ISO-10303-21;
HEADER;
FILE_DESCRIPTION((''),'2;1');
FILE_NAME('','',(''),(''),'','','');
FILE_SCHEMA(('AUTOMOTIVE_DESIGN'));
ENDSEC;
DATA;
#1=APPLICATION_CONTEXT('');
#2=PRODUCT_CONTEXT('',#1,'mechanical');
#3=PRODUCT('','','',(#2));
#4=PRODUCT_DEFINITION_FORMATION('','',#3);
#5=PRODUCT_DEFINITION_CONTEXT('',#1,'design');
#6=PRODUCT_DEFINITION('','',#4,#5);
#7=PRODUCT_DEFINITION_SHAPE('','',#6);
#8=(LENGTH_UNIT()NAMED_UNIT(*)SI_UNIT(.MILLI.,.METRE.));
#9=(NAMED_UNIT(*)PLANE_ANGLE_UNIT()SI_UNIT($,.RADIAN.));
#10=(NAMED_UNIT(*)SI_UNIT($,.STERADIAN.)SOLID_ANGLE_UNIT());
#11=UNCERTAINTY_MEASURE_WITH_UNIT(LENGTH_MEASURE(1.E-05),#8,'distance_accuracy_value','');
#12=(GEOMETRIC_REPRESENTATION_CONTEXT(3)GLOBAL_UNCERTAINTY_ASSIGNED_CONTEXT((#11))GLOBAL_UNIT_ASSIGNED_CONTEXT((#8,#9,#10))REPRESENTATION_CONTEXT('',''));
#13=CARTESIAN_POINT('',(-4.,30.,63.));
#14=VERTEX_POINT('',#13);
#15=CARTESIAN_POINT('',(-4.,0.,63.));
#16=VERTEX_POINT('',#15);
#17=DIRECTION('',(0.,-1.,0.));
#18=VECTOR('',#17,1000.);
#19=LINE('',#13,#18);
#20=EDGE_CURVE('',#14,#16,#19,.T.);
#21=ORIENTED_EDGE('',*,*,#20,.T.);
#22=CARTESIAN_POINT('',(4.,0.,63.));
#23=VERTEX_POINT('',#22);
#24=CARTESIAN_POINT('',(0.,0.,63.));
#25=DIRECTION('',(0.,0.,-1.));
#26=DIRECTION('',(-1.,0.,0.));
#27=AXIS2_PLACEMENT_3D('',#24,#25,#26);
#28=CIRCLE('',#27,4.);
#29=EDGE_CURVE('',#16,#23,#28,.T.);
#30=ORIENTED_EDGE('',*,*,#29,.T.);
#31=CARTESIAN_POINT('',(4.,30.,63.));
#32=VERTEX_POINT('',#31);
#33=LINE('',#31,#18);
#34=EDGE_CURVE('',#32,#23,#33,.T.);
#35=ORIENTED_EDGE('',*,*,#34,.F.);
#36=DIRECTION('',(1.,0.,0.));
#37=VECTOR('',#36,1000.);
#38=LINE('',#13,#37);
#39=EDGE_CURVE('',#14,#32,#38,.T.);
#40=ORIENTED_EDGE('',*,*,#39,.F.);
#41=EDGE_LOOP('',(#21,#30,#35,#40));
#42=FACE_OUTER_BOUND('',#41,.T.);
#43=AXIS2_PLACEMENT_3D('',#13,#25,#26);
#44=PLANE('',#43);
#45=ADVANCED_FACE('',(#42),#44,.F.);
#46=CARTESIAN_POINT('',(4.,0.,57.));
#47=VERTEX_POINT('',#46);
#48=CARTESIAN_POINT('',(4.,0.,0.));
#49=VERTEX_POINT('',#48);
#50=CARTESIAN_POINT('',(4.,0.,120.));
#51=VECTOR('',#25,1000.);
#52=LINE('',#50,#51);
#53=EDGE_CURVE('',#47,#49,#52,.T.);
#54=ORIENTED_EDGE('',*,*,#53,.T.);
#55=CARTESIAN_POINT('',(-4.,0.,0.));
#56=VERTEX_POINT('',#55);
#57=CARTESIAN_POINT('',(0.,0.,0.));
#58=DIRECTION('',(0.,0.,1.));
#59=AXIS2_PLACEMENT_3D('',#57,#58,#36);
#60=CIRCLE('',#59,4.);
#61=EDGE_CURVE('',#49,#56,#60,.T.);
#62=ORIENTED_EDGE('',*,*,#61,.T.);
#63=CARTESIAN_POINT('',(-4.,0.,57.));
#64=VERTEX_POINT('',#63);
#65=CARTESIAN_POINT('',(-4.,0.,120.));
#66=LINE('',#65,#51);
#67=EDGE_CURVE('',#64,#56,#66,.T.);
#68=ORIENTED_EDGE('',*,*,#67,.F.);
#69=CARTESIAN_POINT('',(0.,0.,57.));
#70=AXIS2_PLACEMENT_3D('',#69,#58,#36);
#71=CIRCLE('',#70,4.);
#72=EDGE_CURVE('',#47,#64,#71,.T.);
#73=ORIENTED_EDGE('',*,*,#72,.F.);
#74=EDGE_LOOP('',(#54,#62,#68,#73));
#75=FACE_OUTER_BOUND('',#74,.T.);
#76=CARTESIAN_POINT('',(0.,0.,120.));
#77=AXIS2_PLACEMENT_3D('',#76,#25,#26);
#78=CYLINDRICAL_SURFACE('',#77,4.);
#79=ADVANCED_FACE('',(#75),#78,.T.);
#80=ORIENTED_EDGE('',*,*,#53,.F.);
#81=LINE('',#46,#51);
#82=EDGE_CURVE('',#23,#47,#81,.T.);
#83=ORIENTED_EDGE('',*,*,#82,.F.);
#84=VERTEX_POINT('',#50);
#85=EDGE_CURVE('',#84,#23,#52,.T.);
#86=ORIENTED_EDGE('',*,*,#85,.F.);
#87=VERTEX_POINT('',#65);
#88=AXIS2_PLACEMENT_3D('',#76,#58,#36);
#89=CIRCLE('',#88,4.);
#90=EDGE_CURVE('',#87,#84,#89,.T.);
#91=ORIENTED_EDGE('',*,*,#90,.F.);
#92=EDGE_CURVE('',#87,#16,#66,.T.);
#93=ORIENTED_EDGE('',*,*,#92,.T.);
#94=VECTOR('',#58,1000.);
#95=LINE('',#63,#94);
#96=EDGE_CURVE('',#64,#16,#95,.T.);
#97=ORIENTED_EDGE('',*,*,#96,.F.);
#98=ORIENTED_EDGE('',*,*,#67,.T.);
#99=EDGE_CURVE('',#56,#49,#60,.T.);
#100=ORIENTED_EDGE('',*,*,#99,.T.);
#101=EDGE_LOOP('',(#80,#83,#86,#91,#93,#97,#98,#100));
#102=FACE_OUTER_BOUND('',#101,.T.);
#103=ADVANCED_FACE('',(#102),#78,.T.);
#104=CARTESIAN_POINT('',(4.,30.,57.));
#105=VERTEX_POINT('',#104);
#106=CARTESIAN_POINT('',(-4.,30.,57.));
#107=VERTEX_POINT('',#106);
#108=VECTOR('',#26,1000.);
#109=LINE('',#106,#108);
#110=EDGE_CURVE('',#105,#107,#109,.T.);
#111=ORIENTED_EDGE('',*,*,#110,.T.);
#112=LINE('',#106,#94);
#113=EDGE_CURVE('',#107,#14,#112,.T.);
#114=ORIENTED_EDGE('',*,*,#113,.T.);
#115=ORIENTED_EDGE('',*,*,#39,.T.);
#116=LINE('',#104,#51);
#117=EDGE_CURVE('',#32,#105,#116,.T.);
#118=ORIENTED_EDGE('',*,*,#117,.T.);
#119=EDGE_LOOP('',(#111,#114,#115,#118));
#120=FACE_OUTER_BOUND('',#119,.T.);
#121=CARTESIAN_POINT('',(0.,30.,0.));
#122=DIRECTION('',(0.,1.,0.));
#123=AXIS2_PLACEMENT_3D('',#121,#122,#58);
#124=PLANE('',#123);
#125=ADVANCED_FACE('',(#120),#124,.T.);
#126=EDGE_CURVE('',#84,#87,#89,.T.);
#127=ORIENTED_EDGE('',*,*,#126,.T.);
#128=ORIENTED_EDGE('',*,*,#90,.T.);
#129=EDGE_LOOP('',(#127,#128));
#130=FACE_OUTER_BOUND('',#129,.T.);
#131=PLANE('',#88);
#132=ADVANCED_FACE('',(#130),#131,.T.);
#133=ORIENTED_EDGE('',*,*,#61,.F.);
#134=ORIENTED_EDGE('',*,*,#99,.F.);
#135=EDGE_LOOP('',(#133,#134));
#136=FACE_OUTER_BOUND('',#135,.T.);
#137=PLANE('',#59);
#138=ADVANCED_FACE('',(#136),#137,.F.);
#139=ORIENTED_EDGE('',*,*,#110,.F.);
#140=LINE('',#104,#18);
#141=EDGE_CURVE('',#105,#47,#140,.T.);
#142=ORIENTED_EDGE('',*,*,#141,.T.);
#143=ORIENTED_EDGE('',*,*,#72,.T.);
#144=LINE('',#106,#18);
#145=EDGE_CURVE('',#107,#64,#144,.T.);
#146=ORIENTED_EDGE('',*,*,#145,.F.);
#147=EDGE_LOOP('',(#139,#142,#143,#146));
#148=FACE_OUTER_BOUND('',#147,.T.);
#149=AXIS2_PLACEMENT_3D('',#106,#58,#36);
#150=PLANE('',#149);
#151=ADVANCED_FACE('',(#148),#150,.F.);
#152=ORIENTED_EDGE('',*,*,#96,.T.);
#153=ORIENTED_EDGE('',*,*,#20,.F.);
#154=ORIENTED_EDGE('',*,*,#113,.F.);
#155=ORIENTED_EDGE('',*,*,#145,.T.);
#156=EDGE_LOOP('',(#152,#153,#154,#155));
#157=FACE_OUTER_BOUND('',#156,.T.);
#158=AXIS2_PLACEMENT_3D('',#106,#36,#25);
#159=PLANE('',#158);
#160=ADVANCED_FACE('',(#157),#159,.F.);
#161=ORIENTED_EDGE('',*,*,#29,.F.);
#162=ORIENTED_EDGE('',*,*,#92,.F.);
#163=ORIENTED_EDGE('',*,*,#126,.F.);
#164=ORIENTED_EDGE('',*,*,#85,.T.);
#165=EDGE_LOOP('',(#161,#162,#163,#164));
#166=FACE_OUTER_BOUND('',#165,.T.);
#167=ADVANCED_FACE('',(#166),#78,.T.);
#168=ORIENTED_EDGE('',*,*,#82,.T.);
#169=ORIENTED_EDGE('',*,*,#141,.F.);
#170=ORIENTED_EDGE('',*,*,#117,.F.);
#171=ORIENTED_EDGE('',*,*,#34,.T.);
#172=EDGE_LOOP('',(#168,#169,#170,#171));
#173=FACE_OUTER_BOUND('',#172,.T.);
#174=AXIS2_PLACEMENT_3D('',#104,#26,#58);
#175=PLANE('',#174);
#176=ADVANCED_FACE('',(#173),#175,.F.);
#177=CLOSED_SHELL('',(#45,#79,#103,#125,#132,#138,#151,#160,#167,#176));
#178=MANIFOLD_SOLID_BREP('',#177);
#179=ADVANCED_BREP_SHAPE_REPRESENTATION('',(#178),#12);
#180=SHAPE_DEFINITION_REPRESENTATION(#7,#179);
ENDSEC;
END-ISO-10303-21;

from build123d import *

# Parameters (mm, degrees)
SKETCH1_R           = 4
BOSS_EXTRUDE1_DEPTH = 120
SKETCH2_W           = 8
SKETCH2_H           = 6
BOSS_EXTRUDE2_DEPTH = 30


with BuildPart() as part:
    # Sketch1 → Boss-Extrude1 (new body)
    with BuildSketch(Plane.XY):
        with Locations(Location((0, 0, 0), (0, 0, 180))):
            Circle(SKETCH1_R)
    extrude(amount=BOSS_EXTRUDE1_DEPTH)

    # Sketch2 → Boss-Extrude2 (add)
    with BuildSketch(Plane(origin=(0, 0, 0), x_dir=(1, 0, 0), z_dir=(0, 1, 0))):
        with Locations((0, -60)):
            Rectangle(SKETCH2_W, SKETCH2_H)
    extrude(amount=BOSS_EXTRUDE2_DEPTH)


solid = part.part
